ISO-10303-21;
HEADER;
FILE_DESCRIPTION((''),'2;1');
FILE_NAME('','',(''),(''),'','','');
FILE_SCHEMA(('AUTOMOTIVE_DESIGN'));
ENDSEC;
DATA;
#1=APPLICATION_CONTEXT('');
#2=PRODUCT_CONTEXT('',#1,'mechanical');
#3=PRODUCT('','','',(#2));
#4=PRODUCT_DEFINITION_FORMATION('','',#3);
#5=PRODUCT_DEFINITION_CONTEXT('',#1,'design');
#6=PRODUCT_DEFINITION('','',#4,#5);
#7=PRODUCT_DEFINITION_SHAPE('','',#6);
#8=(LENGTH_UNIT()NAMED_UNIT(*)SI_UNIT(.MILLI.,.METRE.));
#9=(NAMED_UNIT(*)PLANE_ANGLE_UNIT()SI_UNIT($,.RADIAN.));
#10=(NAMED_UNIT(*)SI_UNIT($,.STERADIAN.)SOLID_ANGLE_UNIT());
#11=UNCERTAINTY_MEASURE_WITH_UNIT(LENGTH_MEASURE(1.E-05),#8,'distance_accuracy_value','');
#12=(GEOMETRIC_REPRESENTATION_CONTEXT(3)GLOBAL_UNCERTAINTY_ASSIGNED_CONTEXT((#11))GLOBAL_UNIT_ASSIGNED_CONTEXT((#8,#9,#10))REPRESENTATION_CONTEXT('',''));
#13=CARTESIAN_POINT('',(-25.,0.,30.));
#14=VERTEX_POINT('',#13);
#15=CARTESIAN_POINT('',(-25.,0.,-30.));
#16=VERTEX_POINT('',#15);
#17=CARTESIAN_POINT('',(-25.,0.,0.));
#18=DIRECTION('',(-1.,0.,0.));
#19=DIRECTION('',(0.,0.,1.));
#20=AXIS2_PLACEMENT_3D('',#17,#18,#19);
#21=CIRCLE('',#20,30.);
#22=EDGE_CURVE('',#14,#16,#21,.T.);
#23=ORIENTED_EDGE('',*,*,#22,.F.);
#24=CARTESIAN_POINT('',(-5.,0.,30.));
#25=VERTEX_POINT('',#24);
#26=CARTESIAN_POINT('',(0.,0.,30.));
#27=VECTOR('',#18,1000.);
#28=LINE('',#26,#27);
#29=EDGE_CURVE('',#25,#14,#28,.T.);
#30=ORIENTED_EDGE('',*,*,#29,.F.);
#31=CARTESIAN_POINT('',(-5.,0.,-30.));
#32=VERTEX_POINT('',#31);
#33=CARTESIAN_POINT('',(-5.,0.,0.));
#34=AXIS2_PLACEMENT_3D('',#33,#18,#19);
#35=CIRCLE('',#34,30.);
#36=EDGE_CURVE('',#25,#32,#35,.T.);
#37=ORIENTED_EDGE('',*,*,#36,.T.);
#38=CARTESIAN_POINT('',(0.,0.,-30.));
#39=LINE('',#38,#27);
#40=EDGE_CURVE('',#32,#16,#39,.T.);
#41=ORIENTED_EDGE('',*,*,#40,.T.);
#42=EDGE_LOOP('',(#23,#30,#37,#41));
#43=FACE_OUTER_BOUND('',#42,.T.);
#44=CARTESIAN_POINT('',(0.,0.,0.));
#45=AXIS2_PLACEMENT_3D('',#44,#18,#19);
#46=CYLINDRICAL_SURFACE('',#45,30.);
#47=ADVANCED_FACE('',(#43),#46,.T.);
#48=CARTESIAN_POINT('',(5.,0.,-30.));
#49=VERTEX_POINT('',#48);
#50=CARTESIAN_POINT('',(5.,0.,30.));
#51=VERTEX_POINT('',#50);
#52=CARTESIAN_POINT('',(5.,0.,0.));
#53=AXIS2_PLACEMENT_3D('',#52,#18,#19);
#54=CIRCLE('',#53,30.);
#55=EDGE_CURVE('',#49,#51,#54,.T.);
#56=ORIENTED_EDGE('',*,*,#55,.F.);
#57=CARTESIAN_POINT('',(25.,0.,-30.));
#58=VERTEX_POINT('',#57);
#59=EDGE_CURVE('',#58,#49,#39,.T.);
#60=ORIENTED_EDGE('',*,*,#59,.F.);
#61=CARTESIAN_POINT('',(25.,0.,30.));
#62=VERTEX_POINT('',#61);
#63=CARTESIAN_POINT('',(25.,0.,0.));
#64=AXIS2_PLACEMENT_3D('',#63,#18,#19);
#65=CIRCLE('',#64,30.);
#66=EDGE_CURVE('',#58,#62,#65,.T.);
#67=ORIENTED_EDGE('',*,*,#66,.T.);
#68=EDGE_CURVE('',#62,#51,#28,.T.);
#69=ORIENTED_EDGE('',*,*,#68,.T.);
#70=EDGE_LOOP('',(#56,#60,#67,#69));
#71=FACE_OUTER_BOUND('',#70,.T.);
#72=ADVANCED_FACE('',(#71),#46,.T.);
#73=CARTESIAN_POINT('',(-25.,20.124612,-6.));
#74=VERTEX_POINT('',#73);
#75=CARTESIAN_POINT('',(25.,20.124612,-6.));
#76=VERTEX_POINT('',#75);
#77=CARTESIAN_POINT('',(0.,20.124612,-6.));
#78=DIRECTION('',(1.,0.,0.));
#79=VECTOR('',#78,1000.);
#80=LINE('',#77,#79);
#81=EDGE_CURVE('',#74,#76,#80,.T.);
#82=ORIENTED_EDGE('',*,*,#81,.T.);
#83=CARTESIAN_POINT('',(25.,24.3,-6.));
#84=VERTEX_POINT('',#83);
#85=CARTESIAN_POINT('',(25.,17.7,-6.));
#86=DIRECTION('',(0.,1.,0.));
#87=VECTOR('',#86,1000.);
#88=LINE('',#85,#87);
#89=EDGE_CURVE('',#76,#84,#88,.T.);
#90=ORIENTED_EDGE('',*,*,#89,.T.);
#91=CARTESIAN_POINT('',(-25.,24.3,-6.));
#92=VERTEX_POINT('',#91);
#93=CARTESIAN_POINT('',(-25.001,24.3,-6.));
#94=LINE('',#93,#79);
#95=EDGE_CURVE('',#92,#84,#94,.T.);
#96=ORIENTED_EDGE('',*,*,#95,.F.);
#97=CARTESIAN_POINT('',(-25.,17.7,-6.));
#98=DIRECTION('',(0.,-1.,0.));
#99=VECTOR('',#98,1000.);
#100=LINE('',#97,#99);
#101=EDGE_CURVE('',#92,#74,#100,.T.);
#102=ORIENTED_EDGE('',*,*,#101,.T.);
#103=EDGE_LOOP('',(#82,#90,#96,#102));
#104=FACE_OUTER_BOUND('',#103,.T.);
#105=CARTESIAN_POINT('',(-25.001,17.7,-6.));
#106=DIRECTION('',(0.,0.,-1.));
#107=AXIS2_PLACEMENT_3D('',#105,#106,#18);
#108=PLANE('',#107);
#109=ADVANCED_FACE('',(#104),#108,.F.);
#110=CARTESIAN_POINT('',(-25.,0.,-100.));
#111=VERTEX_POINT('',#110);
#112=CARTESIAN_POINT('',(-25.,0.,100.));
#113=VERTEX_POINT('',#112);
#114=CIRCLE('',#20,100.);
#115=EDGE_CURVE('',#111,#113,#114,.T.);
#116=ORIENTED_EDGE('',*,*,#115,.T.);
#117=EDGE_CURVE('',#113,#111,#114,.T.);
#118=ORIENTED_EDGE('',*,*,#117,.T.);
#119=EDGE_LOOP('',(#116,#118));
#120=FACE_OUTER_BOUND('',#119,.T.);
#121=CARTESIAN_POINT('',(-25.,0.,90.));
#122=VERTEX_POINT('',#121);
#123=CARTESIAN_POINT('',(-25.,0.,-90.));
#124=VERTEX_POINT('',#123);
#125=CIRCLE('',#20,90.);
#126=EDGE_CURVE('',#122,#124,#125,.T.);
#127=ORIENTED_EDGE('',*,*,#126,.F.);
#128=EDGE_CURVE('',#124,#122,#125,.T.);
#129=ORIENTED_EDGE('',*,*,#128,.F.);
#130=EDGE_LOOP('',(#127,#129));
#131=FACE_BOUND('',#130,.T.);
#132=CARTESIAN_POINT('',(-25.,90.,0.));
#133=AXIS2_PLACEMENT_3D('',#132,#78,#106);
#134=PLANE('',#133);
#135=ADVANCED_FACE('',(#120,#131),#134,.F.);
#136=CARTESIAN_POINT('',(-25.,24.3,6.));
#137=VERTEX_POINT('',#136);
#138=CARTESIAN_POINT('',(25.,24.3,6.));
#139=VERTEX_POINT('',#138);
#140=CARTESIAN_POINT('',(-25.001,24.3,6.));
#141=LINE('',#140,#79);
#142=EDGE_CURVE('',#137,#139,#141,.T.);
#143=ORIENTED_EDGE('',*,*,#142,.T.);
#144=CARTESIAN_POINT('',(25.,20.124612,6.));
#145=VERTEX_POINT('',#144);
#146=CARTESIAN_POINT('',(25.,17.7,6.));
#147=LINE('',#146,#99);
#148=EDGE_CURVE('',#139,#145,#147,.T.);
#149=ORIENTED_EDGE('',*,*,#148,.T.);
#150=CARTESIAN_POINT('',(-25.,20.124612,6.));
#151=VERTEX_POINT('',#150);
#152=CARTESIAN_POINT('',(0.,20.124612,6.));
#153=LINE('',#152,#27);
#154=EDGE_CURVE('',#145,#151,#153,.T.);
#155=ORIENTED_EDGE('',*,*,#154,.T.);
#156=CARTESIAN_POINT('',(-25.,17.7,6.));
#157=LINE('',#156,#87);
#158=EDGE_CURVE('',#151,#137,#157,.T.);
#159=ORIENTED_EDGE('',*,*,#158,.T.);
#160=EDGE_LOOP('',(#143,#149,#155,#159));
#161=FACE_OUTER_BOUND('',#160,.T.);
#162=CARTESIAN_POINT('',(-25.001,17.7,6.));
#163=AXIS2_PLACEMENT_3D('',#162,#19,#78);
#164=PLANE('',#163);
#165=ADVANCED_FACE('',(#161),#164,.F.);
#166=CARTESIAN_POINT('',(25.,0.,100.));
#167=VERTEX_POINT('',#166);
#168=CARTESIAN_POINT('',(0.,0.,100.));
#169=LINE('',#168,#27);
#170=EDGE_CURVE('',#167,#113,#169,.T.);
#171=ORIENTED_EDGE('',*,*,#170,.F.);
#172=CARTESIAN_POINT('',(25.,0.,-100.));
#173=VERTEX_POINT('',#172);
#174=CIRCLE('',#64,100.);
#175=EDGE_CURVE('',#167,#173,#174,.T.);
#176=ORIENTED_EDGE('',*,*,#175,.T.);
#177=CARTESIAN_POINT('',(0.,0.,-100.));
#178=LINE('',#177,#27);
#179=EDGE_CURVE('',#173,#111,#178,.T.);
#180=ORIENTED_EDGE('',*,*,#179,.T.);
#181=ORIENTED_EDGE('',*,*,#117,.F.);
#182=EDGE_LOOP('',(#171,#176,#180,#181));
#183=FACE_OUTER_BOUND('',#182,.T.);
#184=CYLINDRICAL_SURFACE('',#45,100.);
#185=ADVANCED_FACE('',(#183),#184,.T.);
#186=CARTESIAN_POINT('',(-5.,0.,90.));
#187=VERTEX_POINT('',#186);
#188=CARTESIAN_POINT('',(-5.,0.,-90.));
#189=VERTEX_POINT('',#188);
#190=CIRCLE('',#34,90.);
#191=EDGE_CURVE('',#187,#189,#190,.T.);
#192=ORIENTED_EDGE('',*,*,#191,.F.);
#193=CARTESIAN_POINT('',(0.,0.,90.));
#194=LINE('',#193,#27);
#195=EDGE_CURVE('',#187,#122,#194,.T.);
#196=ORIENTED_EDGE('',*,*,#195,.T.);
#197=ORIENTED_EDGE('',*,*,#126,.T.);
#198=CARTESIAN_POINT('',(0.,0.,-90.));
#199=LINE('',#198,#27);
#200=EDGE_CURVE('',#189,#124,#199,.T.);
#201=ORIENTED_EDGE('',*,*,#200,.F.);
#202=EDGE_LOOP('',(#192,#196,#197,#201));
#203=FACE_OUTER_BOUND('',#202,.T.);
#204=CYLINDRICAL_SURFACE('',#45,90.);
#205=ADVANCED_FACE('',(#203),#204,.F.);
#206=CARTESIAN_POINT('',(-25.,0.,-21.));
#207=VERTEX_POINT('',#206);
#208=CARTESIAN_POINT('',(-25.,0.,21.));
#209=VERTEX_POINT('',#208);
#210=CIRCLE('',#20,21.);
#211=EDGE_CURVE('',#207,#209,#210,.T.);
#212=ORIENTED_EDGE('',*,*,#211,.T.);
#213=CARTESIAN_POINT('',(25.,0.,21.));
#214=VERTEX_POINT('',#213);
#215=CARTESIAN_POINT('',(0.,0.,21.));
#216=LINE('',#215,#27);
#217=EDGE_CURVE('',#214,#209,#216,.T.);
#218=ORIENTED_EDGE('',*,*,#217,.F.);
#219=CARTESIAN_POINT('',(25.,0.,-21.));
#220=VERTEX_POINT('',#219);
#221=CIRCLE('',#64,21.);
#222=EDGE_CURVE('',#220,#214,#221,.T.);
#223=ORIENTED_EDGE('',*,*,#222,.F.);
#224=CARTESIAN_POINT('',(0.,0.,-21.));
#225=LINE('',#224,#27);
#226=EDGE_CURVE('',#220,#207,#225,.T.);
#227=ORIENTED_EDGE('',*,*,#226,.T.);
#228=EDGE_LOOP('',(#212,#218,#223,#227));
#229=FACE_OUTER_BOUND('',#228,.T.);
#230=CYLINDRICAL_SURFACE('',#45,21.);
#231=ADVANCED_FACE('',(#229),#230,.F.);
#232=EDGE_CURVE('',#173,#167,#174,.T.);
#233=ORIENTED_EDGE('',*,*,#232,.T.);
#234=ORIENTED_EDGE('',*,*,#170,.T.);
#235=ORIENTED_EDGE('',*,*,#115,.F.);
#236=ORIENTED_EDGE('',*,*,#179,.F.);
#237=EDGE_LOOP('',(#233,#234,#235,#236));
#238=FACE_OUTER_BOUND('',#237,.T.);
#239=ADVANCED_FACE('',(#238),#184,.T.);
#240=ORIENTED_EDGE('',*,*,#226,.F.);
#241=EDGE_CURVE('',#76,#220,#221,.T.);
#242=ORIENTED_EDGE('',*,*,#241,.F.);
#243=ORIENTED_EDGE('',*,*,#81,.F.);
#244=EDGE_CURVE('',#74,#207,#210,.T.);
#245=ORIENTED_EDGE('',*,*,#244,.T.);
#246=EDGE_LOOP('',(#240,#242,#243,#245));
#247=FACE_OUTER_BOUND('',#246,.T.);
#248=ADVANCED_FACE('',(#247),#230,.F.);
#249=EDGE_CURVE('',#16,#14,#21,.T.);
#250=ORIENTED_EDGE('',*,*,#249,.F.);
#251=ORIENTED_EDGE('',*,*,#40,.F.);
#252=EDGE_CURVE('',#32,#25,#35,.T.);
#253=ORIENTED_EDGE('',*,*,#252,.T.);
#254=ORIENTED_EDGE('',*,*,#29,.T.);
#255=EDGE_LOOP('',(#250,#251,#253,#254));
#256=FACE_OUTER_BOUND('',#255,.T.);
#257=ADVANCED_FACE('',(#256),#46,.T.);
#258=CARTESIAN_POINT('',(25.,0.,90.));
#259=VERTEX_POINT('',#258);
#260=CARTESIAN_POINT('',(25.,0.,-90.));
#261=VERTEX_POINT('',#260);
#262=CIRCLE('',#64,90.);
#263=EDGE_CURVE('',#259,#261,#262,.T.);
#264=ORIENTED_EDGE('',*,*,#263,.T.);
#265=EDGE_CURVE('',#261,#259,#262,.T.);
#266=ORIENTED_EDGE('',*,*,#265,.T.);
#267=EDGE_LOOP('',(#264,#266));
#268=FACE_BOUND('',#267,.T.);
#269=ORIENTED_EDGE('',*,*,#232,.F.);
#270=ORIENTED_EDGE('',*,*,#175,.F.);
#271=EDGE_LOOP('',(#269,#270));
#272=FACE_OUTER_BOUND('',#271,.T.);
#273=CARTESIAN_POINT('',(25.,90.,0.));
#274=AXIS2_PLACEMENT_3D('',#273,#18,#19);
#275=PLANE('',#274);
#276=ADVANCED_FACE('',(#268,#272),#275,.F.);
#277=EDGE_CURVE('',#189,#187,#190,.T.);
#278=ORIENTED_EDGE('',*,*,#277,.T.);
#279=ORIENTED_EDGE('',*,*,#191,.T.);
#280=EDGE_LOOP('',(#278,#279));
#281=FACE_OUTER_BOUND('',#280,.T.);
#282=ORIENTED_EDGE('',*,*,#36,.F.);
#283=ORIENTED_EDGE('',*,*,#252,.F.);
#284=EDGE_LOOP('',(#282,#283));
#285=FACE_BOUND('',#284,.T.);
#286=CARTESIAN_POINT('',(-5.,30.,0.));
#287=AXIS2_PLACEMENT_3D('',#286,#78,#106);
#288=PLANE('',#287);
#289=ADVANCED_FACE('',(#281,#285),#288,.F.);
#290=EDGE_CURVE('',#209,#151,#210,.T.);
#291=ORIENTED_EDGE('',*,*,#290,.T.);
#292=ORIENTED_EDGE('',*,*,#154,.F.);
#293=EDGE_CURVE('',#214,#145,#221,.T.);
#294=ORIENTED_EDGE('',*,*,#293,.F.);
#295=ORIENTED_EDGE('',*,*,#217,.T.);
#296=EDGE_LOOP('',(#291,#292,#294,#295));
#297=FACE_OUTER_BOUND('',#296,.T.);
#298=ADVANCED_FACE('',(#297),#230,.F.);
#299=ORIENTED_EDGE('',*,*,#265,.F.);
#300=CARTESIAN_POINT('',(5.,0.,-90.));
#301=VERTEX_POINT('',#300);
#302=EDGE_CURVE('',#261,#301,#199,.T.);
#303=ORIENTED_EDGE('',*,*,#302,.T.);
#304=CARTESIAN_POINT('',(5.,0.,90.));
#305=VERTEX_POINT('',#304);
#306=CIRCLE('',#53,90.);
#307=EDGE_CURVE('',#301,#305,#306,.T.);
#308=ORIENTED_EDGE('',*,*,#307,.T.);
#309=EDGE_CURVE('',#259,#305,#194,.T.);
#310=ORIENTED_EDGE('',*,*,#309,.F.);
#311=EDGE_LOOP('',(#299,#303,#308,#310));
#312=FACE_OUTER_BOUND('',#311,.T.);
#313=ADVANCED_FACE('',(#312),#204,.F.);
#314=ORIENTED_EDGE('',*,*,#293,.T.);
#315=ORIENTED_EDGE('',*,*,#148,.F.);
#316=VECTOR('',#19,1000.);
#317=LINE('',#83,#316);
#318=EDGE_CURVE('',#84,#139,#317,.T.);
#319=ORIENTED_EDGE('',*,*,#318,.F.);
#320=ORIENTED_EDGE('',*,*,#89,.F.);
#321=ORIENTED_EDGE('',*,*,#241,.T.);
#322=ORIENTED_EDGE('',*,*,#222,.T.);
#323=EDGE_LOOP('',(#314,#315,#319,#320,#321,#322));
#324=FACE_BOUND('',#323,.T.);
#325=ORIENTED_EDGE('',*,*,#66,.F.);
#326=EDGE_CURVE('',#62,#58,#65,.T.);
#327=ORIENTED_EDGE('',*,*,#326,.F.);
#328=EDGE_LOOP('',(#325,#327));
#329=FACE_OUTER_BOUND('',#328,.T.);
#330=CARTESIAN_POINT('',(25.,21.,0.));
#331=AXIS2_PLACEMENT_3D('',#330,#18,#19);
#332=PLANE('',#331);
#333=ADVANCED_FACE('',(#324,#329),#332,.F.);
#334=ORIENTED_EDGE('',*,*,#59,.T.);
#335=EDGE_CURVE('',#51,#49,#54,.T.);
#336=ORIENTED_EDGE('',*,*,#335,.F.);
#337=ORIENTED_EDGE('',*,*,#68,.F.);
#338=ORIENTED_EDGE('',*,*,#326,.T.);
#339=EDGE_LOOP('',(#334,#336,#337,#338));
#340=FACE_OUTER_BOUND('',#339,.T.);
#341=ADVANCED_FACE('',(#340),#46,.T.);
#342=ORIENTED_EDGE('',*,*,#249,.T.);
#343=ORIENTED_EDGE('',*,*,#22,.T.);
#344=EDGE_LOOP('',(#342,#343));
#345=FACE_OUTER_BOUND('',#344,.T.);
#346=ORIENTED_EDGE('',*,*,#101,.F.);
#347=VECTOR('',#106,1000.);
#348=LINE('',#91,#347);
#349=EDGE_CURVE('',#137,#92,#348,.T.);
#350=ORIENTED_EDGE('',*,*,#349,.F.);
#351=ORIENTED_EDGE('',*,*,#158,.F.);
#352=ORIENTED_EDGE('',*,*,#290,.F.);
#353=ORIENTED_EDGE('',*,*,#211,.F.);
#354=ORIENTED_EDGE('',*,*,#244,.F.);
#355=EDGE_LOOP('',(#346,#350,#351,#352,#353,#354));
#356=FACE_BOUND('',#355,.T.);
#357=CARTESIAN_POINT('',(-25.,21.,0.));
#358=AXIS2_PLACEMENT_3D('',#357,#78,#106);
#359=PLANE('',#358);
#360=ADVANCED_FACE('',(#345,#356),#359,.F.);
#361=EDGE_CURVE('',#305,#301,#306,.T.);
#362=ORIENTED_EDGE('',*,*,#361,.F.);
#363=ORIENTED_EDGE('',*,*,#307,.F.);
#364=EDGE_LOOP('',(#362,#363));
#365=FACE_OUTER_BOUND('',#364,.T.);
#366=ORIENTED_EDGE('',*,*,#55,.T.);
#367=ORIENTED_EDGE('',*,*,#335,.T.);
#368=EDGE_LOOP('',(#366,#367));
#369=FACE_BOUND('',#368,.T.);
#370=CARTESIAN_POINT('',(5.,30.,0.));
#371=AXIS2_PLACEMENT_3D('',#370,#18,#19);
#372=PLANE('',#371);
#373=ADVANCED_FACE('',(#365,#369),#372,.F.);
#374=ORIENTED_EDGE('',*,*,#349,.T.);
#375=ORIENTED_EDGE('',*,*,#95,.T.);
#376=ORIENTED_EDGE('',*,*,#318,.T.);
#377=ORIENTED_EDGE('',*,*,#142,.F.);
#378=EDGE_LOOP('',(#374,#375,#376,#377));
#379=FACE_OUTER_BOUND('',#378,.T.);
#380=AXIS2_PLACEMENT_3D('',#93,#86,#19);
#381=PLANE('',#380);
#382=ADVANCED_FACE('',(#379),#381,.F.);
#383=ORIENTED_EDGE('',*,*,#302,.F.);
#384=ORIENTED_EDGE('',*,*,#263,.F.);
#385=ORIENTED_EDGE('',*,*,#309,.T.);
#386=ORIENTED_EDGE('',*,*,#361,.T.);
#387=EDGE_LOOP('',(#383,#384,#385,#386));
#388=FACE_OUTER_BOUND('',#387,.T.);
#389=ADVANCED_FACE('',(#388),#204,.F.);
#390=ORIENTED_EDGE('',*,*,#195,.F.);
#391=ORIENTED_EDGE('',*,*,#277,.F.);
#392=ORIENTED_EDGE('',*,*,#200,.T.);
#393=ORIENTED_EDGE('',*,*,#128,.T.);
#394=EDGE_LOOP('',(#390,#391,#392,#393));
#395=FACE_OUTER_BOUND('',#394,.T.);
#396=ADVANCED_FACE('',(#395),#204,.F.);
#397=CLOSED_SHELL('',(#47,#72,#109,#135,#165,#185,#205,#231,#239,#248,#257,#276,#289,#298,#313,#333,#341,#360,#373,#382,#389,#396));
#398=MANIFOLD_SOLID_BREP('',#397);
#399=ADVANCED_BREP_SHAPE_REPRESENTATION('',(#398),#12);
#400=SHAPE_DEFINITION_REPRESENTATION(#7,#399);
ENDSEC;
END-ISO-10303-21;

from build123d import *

# Parameters (mm, degrees)
CUT_EXTRUDE1_REACH = 152
SKETCH2_W          = 12
SKETCH2_H          = 6.6


with BuildPart() as part:
    # Sketch1 → Revolve1 (revolve)
    with BuildSketch(Plane.XY, mode=Mode.PRIVATE) as revolve1_sk:
        Polygon((-25, 21), (25, 21), (25, 30), (5, 30), (5, 90), (25, 90), (25, 100), (-25, 100), (-25, 90), (-5, 90), (-5, 30), (-25, 30), align=None)
    revolve(revolve1_sk.sketch.rotate(Axis((0, 0, 0), (1, 0, 0)), 90), axis=Axis((0, 0, 0), (1, 0, 0)))

    # Sketch2 → Cut-Extrude1 (cut, up to next)
    with BuildSketch(Plane(origin=(25, 0, 0), x_dir=(0, 0, -1), z_dir=(1, 0, 0)), mode=Mode.PRIVATE) as cut_extrude1_sk1:
        with Locations((0, 21)):
            Rectangle(SKETCH2_W, SKETCH2_H)
    cut_extrude1_tool1 = extrude(cut_extrude1_sk1.sketch, amount=-CUT_EXTRUDE1_REACH, mode=Mode.PRIVATE) & part.part
    add(cut_extrude1_tool1.solids().sort_by_distance((25, 21, 0))[0], mode=Mode.SUBTRACT)


solid = part.part
